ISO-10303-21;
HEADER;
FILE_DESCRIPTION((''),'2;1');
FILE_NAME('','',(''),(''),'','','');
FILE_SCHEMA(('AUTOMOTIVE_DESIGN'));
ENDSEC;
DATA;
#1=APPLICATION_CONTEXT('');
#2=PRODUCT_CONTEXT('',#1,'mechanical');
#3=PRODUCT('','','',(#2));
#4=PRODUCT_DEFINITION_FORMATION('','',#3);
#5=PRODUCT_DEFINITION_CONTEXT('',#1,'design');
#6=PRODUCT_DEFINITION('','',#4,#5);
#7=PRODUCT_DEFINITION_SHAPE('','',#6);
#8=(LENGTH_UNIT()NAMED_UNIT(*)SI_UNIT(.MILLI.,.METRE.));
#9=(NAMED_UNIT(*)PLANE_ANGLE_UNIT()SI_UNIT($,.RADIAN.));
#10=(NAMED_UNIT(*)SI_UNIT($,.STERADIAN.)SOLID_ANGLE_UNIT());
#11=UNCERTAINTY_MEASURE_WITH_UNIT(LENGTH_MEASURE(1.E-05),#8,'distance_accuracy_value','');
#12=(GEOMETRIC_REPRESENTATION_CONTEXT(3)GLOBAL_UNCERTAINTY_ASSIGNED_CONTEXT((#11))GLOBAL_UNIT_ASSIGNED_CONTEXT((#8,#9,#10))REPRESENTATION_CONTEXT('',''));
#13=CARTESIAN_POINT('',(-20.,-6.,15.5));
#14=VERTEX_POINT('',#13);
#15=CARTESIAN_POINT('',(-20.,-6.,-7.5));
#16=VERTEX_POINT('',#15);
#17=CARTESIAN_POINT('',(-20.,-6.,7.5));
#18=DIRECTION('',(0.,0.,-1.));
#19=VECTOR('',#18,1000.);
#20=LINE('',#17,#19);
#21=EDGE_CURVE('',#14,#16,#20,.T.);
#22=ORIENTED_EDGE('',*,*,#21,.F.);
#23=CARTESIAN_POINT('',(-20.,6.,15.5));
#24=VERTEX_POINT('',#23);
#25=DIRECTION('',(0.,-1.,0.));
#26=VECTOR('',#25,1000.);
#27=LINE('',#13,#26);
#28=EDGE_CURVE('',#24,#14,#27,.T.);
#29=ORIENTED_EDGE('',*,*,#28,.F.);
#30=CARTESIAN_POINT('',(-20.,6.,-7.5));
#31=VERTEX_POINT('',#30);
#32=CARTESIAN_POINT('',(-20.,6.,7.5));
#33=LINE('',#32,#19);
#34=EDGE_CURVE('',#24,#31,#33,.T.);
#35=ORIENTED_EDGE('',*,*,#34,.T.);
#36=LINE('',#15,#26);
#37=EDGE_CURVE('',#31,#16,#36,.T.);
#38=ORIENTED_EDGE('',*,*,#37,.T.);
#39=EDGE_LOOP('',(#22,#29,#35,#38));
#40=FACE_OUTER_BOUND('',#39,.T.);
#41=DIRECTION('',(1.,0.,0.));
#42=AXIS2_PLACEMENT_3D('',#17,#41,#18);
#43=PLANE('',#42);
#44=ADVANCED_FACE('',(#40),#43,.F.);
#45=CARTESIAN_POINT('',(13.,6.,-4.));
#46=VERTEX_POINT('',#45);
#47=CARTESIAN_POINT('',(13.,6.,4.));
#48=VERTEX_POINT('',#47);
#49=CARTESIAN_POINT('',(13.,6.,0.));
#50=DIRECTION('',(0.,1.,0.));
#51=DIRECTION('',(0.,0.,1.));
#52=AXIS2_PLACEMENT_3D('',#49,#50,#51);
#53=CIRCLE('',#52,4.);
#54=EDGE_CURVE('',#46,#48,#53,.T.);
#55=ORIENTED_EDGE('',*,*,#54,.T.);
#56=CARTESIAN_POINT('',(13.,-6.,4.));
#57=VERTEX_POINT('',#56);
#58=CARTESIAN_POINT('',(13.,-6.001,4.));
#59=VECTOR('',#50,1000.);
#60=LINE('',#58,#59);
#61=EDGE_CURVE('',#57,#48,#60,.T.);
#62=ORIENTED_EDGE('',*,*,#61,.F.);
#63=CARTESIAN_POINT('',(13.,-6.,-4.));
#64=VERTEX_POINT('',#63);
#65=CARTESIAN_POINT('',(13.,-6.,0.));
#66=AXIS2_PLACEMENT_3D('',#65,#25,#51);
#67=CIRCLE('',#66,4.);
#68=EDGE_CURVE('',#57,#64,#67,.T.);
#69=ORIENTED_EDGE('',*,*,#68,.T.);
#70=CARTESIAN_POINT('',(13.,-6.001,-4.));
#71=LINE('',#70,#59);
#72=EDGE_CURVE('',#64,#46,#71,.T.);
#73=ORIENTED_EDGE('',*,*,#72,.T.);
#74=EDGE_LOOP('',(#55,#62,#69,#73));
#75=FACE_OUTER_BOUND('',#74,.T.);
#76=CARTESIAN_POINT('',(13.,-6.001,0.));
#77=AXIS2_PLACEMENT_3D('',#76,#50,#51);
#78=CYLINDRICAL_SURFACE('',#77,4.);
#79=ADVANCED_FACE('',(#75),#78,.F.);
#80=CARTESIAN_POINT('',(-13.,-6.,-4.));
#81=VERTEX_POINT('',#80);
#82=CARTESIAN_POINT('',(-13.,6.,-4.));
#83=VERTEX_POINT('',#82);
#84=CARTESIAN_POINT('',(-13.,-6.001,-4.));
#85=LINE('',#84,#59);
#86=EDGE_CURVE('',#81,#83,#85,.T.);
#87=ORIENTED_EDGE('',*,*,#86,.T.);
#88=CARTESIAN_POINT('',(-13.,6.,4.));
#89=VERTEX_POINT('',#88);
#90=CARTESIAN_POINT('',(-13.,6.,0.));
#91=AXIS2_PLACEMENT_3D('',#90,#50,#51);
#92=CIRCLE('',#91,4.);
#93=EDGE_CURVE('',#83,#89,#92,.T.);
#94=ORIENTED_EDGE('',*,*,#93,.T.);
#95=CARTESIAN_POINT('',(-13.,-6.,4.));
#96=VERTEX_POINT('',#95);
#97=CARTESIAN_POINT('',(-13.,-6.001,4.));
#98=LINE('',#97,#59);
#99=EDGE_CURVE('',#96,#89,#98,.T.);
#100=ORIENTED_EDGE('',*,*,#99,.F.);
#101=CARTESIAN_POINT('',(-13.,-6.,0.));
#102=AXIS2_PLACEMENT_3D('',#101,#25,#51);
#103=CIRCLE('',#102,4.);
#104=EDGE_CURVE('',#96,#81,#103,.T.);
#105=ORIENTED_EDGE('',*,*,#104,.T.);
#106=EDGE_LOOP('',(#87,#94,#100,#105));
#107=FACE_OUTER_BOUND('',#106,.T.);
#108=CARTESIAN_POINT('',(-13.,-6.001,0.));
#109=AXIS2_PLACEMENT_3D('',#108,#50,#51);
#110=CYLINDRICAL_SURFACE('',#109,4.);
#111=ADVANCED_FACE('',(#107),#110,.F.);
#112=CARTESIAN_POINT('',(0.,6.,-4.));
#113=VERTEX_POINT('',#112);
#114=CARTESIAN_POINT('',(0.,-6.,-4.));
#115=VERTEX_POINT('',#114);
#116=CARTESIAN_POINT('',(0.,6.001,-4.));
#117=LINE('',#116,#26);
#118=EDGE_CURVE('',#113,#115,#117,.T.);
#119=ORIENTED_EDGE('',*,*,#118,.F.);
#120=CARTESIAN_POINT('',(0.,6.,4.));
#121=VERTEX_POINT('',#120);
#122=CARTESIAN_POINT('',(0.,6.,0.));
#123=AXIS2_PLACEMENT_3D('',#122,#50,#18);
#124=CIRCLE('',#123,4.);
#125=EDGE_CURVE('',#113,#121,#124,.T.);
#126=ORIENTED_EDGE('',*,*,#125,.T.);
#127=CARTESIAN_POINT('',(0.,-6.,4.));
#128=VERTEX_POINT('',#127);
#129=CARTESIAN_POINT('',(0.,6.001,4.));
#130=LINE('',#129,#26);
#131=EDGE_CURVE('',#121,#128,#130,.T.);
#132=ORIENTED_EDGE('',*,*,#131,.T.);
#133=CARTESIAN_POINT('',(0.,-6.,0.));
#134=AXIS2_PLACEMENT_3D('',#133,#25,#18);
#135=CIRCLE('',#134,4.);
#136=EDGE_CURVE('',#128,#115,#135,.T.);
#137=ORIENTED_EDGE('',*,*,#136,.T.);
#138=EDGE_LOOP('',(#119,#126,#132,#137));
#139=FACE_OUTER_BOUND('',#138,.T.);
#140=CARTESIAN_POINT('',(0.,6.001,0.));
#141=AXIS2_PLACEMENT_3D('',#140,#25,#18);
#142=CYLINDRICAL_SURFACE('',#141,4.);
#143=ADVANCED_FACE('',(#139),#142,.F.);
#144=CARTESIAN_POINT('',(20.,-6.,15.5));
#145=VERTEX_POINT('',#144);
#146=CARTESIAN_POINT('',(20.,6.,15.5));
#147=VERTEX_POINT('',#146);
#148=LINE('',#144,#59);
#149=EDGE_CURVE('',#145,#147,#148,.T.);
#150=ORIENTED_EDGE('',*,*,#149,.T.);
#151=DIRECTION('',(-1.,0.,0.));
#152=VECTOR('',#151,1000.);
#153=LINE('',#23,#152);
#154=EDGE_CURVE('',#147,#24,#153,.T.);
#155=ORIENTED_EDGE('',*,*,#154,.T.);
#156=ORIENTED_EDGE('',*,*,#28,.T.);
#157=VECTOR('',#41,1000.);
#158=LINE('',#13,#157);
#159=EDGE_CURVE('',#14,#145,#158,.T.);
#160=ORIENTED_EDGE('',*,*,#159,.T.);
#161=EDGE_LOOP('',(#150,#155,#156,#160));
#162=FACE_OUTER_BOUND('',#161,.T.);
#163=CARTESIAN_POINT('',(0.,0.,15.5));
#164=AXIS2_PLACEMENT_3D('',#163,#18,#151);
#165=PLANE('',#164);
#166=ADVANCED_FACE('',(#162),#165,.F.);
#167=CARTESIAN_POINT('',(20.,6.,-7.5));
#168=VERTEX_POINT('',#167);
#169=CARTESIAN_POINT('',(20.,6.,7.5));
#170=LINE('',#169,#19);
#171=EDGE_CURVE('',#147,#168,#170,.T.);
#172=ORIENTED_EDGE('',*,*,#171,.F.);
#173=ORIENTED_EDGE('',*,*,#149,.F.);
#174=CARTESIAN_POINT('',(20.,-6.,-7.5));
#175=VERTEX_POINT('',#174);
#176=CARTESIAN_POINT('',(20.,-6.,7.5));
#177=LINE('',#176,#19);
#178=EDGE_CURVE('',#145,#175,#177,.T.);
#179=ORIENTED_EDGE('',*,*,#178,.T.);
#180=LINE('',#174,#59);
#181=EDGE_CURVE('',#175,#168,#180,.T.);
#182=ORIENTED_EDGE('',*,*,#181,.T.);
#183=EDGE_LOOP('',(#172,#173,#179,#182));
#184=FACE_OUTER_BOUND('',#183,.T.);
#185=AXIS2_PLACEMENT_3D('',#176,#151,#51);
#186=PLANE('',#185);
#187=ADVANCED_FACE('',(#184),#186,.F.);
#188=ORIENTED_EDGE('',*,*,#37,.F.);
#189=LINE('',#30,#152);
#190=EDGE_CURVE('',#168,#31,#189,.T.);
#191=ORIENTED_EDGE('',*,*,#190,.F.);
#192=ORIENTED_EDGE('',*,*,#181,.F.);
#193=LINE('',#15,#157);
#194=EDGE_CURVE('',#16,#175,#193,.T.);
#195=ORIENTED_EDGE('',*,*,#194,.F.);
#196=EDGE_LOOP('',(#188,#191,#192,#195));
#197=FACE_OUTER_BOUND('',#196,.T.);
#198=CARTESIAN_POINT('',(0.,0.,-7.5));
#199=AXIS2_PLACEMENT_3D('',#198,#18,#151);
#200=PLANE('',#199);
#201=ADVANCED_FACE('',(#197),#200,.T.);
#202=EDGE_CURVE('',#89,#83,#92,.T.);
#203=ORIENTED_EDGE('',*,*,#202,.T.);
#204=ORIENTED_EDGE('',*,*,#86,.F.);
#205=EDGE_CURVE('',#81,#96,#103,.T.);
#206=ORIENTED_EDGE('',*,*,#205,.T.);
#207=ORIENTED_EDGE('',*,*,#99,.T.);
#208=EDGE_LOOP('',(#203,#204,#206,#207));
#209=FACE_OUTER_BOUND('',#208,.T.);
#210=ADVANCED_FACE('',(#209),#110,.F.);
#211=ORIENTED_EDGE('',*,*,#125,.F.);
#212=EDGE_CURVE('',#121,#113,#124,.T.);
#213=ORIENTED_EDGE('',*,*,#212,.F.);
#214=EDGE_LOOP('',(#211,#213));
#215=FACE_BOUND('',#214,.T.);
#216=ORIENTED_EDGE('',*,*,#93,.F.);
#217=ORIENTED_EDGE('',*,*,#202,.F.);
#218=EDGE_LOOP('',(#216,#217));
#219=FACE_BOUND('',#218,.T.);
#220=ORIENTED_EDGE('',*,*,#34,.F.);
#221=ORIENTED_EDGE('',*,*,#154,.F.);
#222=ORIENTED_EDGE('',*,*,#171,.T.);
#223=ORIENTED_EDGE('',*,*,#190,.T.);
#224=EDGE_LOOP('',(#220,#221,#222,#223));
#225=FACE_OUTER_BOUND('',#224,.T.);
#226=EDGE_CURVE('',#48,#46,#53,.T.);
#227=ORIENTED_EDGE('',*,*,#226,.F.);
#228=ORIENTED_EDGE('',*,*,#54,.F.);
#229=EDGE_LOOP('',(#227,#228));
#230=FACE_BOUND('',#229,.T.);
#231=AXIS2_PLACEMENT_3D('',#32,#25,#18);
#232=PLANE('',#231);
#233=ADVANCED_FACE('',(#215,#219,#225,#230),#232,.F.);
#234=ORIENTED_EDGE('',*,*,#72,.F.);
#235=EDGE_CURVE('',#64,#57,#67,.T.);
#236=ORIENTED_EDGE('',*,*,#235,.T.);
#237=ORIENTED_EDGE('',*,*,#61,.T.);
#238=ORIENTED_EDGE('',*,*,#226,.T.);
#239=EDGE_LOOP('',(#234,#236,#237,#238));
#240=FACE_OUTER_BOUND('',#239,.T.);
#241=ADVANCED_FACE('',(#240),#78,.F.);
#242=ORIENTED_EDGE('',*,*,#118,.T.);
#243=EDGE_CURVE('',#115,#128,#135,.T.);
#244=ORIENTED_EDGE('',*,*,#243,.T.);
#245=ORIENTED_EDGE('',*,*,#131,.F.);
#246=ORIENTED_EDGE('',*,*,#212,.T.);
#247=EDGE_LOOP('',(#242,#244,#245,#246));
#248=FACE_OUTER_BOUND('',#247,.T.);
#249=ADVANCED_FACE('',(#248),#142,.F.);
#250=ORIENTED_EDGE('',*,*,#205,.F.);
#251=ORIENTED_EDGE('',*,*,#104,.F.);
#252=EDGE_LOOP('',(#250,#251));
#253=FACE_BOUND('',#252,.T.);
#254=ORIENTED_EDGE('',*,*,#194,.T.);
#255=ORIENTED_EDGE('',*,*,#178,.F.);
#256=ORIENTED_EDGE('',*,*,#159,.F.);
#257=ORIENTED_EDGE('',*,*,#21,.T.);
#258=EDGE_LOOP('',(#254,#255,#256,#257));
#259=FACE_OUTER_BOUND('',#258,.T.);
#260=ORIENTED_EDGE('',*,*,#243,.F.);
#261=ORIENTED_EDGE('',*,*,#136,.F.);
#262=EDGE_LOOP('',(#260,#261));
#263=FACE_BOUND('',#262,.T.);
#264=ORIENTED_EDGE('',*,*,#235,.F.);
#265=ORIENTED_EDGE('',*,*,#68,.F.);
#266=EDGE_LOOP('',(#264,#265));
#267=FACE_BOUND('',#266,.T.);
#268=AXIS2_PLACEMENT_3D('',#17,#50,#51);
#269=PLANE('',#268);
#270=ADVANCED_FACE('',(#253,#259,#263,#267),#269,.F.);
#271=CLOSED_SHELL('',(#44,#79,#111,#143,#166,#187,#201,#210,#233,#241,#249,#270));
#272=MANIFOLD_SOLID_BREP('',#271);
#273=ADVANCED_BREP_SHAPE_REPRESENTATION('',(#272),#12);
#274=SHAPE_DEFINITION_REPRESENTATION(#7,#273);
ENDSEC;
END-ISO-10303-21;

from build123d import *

# Parameters (mm, degrees)
SKETCH_1_W          = 40
SKETCH_1_H          = 12
EXTRUDE_1_DEPTH     = 7.5
CUT_EXTRUDE_1_REACH = 26.5
SKETCH_2_R          = 4
CUT_EXTRUDE_2_REACH = 26.5
SKETCH_3_R          = 4
SKETCH_6_W          = 40
SKETCH_6_H          = 12
EXTRUDE_3_DEPTH     = 8


with BuildPart() as part:
    # 草图1 → 凸台-拉伸1 (new, symmetric)
    with BuildSketch(Plane.XY):
        Rectangle(SKETCH_1_W, SKETCH_1_H)
    extrude(amount=EXTRUDE_1_DEPTH, both=True)

    # 草图2 → 切除-拉伸1 (cut, up to next)
    with BuildSketch(Plane(origin=(0, 6, 0), x_dir=(1, 0, 0), z_dir=(0, 1, 0)), mode=Mode.PRIVATE) as cut_extrude_1_sk1:
        with Locations(Location((-13, 0, 0), (0, 0, 270))):
            Circle(SKETCH_2_R)
    cut_extrude_1_tool1 = extrude(cut_extrude_1_sk1.sketch, amount=-CUT_EXTRUDE_1_REACH, mode=Mode.PRIVATE) & part.part
    # 草图2 → 切除-拉伸1 (cut, up to next)
    with BuildSketch(Plane(origin=(0, 6, 0), x_dir=(1, 0, 0), z_dir=(0, 1, 0)), mode=Mode.PRIVATE) as cut_extrude_1_sk2:
        with Locations(Location((13, 0, 0), (0, 0, 270))):
            Circle(SKETCH_2_R)
    cut_extrude_1_tool2 = extrude(cut_extrude_1_sk2.sketch, amount=-CUT_EXTRUDE_1_REACH, mode=Mode.PRIVATE) & part.part
    add(cut_extrude_1_tool1.solids().sort_by_distance((-13, 6, 0))[0], mode=Mode.SUBTRACT)
    add(cut_extrude_1_tool2.solids().sort_by_distance((13, 6, 0))[0], mode=Mode.SUBTRACT)

    # 草图3 → 切除-拉伸2 (cut, up to next)
    with BuildSketch(Plane.XZ.offset(6), mode=Mode.PRIVATE) as cut_extrude_2_sk1:
        with Locations(Location((0, 0, 0), (0, 0, 270))):
            Circle(SKETCH_3_R)
    cut_extrude_2_tool1 = extrude(cut_extrude_2_sk1.sketch, amount=-CUT_EXTRUDE_2_REACH, mode=Mode.PRIVATE) & part.part
    add(cut_extrude_2_tool1.solids().sort_by_distance((0, -6, 0))[0], mode=Mode.SUBTRACT)

    # 草图6 → 凸台-拉伸3 (add)
    with BuildSketch(Plane.XY.offset(7.5)):
        Rectangle(SKETCH_6_W, SKETCH_6_H)
    extrude(amount=EXTRUDE_3_DEPTH)


solid = part.part
